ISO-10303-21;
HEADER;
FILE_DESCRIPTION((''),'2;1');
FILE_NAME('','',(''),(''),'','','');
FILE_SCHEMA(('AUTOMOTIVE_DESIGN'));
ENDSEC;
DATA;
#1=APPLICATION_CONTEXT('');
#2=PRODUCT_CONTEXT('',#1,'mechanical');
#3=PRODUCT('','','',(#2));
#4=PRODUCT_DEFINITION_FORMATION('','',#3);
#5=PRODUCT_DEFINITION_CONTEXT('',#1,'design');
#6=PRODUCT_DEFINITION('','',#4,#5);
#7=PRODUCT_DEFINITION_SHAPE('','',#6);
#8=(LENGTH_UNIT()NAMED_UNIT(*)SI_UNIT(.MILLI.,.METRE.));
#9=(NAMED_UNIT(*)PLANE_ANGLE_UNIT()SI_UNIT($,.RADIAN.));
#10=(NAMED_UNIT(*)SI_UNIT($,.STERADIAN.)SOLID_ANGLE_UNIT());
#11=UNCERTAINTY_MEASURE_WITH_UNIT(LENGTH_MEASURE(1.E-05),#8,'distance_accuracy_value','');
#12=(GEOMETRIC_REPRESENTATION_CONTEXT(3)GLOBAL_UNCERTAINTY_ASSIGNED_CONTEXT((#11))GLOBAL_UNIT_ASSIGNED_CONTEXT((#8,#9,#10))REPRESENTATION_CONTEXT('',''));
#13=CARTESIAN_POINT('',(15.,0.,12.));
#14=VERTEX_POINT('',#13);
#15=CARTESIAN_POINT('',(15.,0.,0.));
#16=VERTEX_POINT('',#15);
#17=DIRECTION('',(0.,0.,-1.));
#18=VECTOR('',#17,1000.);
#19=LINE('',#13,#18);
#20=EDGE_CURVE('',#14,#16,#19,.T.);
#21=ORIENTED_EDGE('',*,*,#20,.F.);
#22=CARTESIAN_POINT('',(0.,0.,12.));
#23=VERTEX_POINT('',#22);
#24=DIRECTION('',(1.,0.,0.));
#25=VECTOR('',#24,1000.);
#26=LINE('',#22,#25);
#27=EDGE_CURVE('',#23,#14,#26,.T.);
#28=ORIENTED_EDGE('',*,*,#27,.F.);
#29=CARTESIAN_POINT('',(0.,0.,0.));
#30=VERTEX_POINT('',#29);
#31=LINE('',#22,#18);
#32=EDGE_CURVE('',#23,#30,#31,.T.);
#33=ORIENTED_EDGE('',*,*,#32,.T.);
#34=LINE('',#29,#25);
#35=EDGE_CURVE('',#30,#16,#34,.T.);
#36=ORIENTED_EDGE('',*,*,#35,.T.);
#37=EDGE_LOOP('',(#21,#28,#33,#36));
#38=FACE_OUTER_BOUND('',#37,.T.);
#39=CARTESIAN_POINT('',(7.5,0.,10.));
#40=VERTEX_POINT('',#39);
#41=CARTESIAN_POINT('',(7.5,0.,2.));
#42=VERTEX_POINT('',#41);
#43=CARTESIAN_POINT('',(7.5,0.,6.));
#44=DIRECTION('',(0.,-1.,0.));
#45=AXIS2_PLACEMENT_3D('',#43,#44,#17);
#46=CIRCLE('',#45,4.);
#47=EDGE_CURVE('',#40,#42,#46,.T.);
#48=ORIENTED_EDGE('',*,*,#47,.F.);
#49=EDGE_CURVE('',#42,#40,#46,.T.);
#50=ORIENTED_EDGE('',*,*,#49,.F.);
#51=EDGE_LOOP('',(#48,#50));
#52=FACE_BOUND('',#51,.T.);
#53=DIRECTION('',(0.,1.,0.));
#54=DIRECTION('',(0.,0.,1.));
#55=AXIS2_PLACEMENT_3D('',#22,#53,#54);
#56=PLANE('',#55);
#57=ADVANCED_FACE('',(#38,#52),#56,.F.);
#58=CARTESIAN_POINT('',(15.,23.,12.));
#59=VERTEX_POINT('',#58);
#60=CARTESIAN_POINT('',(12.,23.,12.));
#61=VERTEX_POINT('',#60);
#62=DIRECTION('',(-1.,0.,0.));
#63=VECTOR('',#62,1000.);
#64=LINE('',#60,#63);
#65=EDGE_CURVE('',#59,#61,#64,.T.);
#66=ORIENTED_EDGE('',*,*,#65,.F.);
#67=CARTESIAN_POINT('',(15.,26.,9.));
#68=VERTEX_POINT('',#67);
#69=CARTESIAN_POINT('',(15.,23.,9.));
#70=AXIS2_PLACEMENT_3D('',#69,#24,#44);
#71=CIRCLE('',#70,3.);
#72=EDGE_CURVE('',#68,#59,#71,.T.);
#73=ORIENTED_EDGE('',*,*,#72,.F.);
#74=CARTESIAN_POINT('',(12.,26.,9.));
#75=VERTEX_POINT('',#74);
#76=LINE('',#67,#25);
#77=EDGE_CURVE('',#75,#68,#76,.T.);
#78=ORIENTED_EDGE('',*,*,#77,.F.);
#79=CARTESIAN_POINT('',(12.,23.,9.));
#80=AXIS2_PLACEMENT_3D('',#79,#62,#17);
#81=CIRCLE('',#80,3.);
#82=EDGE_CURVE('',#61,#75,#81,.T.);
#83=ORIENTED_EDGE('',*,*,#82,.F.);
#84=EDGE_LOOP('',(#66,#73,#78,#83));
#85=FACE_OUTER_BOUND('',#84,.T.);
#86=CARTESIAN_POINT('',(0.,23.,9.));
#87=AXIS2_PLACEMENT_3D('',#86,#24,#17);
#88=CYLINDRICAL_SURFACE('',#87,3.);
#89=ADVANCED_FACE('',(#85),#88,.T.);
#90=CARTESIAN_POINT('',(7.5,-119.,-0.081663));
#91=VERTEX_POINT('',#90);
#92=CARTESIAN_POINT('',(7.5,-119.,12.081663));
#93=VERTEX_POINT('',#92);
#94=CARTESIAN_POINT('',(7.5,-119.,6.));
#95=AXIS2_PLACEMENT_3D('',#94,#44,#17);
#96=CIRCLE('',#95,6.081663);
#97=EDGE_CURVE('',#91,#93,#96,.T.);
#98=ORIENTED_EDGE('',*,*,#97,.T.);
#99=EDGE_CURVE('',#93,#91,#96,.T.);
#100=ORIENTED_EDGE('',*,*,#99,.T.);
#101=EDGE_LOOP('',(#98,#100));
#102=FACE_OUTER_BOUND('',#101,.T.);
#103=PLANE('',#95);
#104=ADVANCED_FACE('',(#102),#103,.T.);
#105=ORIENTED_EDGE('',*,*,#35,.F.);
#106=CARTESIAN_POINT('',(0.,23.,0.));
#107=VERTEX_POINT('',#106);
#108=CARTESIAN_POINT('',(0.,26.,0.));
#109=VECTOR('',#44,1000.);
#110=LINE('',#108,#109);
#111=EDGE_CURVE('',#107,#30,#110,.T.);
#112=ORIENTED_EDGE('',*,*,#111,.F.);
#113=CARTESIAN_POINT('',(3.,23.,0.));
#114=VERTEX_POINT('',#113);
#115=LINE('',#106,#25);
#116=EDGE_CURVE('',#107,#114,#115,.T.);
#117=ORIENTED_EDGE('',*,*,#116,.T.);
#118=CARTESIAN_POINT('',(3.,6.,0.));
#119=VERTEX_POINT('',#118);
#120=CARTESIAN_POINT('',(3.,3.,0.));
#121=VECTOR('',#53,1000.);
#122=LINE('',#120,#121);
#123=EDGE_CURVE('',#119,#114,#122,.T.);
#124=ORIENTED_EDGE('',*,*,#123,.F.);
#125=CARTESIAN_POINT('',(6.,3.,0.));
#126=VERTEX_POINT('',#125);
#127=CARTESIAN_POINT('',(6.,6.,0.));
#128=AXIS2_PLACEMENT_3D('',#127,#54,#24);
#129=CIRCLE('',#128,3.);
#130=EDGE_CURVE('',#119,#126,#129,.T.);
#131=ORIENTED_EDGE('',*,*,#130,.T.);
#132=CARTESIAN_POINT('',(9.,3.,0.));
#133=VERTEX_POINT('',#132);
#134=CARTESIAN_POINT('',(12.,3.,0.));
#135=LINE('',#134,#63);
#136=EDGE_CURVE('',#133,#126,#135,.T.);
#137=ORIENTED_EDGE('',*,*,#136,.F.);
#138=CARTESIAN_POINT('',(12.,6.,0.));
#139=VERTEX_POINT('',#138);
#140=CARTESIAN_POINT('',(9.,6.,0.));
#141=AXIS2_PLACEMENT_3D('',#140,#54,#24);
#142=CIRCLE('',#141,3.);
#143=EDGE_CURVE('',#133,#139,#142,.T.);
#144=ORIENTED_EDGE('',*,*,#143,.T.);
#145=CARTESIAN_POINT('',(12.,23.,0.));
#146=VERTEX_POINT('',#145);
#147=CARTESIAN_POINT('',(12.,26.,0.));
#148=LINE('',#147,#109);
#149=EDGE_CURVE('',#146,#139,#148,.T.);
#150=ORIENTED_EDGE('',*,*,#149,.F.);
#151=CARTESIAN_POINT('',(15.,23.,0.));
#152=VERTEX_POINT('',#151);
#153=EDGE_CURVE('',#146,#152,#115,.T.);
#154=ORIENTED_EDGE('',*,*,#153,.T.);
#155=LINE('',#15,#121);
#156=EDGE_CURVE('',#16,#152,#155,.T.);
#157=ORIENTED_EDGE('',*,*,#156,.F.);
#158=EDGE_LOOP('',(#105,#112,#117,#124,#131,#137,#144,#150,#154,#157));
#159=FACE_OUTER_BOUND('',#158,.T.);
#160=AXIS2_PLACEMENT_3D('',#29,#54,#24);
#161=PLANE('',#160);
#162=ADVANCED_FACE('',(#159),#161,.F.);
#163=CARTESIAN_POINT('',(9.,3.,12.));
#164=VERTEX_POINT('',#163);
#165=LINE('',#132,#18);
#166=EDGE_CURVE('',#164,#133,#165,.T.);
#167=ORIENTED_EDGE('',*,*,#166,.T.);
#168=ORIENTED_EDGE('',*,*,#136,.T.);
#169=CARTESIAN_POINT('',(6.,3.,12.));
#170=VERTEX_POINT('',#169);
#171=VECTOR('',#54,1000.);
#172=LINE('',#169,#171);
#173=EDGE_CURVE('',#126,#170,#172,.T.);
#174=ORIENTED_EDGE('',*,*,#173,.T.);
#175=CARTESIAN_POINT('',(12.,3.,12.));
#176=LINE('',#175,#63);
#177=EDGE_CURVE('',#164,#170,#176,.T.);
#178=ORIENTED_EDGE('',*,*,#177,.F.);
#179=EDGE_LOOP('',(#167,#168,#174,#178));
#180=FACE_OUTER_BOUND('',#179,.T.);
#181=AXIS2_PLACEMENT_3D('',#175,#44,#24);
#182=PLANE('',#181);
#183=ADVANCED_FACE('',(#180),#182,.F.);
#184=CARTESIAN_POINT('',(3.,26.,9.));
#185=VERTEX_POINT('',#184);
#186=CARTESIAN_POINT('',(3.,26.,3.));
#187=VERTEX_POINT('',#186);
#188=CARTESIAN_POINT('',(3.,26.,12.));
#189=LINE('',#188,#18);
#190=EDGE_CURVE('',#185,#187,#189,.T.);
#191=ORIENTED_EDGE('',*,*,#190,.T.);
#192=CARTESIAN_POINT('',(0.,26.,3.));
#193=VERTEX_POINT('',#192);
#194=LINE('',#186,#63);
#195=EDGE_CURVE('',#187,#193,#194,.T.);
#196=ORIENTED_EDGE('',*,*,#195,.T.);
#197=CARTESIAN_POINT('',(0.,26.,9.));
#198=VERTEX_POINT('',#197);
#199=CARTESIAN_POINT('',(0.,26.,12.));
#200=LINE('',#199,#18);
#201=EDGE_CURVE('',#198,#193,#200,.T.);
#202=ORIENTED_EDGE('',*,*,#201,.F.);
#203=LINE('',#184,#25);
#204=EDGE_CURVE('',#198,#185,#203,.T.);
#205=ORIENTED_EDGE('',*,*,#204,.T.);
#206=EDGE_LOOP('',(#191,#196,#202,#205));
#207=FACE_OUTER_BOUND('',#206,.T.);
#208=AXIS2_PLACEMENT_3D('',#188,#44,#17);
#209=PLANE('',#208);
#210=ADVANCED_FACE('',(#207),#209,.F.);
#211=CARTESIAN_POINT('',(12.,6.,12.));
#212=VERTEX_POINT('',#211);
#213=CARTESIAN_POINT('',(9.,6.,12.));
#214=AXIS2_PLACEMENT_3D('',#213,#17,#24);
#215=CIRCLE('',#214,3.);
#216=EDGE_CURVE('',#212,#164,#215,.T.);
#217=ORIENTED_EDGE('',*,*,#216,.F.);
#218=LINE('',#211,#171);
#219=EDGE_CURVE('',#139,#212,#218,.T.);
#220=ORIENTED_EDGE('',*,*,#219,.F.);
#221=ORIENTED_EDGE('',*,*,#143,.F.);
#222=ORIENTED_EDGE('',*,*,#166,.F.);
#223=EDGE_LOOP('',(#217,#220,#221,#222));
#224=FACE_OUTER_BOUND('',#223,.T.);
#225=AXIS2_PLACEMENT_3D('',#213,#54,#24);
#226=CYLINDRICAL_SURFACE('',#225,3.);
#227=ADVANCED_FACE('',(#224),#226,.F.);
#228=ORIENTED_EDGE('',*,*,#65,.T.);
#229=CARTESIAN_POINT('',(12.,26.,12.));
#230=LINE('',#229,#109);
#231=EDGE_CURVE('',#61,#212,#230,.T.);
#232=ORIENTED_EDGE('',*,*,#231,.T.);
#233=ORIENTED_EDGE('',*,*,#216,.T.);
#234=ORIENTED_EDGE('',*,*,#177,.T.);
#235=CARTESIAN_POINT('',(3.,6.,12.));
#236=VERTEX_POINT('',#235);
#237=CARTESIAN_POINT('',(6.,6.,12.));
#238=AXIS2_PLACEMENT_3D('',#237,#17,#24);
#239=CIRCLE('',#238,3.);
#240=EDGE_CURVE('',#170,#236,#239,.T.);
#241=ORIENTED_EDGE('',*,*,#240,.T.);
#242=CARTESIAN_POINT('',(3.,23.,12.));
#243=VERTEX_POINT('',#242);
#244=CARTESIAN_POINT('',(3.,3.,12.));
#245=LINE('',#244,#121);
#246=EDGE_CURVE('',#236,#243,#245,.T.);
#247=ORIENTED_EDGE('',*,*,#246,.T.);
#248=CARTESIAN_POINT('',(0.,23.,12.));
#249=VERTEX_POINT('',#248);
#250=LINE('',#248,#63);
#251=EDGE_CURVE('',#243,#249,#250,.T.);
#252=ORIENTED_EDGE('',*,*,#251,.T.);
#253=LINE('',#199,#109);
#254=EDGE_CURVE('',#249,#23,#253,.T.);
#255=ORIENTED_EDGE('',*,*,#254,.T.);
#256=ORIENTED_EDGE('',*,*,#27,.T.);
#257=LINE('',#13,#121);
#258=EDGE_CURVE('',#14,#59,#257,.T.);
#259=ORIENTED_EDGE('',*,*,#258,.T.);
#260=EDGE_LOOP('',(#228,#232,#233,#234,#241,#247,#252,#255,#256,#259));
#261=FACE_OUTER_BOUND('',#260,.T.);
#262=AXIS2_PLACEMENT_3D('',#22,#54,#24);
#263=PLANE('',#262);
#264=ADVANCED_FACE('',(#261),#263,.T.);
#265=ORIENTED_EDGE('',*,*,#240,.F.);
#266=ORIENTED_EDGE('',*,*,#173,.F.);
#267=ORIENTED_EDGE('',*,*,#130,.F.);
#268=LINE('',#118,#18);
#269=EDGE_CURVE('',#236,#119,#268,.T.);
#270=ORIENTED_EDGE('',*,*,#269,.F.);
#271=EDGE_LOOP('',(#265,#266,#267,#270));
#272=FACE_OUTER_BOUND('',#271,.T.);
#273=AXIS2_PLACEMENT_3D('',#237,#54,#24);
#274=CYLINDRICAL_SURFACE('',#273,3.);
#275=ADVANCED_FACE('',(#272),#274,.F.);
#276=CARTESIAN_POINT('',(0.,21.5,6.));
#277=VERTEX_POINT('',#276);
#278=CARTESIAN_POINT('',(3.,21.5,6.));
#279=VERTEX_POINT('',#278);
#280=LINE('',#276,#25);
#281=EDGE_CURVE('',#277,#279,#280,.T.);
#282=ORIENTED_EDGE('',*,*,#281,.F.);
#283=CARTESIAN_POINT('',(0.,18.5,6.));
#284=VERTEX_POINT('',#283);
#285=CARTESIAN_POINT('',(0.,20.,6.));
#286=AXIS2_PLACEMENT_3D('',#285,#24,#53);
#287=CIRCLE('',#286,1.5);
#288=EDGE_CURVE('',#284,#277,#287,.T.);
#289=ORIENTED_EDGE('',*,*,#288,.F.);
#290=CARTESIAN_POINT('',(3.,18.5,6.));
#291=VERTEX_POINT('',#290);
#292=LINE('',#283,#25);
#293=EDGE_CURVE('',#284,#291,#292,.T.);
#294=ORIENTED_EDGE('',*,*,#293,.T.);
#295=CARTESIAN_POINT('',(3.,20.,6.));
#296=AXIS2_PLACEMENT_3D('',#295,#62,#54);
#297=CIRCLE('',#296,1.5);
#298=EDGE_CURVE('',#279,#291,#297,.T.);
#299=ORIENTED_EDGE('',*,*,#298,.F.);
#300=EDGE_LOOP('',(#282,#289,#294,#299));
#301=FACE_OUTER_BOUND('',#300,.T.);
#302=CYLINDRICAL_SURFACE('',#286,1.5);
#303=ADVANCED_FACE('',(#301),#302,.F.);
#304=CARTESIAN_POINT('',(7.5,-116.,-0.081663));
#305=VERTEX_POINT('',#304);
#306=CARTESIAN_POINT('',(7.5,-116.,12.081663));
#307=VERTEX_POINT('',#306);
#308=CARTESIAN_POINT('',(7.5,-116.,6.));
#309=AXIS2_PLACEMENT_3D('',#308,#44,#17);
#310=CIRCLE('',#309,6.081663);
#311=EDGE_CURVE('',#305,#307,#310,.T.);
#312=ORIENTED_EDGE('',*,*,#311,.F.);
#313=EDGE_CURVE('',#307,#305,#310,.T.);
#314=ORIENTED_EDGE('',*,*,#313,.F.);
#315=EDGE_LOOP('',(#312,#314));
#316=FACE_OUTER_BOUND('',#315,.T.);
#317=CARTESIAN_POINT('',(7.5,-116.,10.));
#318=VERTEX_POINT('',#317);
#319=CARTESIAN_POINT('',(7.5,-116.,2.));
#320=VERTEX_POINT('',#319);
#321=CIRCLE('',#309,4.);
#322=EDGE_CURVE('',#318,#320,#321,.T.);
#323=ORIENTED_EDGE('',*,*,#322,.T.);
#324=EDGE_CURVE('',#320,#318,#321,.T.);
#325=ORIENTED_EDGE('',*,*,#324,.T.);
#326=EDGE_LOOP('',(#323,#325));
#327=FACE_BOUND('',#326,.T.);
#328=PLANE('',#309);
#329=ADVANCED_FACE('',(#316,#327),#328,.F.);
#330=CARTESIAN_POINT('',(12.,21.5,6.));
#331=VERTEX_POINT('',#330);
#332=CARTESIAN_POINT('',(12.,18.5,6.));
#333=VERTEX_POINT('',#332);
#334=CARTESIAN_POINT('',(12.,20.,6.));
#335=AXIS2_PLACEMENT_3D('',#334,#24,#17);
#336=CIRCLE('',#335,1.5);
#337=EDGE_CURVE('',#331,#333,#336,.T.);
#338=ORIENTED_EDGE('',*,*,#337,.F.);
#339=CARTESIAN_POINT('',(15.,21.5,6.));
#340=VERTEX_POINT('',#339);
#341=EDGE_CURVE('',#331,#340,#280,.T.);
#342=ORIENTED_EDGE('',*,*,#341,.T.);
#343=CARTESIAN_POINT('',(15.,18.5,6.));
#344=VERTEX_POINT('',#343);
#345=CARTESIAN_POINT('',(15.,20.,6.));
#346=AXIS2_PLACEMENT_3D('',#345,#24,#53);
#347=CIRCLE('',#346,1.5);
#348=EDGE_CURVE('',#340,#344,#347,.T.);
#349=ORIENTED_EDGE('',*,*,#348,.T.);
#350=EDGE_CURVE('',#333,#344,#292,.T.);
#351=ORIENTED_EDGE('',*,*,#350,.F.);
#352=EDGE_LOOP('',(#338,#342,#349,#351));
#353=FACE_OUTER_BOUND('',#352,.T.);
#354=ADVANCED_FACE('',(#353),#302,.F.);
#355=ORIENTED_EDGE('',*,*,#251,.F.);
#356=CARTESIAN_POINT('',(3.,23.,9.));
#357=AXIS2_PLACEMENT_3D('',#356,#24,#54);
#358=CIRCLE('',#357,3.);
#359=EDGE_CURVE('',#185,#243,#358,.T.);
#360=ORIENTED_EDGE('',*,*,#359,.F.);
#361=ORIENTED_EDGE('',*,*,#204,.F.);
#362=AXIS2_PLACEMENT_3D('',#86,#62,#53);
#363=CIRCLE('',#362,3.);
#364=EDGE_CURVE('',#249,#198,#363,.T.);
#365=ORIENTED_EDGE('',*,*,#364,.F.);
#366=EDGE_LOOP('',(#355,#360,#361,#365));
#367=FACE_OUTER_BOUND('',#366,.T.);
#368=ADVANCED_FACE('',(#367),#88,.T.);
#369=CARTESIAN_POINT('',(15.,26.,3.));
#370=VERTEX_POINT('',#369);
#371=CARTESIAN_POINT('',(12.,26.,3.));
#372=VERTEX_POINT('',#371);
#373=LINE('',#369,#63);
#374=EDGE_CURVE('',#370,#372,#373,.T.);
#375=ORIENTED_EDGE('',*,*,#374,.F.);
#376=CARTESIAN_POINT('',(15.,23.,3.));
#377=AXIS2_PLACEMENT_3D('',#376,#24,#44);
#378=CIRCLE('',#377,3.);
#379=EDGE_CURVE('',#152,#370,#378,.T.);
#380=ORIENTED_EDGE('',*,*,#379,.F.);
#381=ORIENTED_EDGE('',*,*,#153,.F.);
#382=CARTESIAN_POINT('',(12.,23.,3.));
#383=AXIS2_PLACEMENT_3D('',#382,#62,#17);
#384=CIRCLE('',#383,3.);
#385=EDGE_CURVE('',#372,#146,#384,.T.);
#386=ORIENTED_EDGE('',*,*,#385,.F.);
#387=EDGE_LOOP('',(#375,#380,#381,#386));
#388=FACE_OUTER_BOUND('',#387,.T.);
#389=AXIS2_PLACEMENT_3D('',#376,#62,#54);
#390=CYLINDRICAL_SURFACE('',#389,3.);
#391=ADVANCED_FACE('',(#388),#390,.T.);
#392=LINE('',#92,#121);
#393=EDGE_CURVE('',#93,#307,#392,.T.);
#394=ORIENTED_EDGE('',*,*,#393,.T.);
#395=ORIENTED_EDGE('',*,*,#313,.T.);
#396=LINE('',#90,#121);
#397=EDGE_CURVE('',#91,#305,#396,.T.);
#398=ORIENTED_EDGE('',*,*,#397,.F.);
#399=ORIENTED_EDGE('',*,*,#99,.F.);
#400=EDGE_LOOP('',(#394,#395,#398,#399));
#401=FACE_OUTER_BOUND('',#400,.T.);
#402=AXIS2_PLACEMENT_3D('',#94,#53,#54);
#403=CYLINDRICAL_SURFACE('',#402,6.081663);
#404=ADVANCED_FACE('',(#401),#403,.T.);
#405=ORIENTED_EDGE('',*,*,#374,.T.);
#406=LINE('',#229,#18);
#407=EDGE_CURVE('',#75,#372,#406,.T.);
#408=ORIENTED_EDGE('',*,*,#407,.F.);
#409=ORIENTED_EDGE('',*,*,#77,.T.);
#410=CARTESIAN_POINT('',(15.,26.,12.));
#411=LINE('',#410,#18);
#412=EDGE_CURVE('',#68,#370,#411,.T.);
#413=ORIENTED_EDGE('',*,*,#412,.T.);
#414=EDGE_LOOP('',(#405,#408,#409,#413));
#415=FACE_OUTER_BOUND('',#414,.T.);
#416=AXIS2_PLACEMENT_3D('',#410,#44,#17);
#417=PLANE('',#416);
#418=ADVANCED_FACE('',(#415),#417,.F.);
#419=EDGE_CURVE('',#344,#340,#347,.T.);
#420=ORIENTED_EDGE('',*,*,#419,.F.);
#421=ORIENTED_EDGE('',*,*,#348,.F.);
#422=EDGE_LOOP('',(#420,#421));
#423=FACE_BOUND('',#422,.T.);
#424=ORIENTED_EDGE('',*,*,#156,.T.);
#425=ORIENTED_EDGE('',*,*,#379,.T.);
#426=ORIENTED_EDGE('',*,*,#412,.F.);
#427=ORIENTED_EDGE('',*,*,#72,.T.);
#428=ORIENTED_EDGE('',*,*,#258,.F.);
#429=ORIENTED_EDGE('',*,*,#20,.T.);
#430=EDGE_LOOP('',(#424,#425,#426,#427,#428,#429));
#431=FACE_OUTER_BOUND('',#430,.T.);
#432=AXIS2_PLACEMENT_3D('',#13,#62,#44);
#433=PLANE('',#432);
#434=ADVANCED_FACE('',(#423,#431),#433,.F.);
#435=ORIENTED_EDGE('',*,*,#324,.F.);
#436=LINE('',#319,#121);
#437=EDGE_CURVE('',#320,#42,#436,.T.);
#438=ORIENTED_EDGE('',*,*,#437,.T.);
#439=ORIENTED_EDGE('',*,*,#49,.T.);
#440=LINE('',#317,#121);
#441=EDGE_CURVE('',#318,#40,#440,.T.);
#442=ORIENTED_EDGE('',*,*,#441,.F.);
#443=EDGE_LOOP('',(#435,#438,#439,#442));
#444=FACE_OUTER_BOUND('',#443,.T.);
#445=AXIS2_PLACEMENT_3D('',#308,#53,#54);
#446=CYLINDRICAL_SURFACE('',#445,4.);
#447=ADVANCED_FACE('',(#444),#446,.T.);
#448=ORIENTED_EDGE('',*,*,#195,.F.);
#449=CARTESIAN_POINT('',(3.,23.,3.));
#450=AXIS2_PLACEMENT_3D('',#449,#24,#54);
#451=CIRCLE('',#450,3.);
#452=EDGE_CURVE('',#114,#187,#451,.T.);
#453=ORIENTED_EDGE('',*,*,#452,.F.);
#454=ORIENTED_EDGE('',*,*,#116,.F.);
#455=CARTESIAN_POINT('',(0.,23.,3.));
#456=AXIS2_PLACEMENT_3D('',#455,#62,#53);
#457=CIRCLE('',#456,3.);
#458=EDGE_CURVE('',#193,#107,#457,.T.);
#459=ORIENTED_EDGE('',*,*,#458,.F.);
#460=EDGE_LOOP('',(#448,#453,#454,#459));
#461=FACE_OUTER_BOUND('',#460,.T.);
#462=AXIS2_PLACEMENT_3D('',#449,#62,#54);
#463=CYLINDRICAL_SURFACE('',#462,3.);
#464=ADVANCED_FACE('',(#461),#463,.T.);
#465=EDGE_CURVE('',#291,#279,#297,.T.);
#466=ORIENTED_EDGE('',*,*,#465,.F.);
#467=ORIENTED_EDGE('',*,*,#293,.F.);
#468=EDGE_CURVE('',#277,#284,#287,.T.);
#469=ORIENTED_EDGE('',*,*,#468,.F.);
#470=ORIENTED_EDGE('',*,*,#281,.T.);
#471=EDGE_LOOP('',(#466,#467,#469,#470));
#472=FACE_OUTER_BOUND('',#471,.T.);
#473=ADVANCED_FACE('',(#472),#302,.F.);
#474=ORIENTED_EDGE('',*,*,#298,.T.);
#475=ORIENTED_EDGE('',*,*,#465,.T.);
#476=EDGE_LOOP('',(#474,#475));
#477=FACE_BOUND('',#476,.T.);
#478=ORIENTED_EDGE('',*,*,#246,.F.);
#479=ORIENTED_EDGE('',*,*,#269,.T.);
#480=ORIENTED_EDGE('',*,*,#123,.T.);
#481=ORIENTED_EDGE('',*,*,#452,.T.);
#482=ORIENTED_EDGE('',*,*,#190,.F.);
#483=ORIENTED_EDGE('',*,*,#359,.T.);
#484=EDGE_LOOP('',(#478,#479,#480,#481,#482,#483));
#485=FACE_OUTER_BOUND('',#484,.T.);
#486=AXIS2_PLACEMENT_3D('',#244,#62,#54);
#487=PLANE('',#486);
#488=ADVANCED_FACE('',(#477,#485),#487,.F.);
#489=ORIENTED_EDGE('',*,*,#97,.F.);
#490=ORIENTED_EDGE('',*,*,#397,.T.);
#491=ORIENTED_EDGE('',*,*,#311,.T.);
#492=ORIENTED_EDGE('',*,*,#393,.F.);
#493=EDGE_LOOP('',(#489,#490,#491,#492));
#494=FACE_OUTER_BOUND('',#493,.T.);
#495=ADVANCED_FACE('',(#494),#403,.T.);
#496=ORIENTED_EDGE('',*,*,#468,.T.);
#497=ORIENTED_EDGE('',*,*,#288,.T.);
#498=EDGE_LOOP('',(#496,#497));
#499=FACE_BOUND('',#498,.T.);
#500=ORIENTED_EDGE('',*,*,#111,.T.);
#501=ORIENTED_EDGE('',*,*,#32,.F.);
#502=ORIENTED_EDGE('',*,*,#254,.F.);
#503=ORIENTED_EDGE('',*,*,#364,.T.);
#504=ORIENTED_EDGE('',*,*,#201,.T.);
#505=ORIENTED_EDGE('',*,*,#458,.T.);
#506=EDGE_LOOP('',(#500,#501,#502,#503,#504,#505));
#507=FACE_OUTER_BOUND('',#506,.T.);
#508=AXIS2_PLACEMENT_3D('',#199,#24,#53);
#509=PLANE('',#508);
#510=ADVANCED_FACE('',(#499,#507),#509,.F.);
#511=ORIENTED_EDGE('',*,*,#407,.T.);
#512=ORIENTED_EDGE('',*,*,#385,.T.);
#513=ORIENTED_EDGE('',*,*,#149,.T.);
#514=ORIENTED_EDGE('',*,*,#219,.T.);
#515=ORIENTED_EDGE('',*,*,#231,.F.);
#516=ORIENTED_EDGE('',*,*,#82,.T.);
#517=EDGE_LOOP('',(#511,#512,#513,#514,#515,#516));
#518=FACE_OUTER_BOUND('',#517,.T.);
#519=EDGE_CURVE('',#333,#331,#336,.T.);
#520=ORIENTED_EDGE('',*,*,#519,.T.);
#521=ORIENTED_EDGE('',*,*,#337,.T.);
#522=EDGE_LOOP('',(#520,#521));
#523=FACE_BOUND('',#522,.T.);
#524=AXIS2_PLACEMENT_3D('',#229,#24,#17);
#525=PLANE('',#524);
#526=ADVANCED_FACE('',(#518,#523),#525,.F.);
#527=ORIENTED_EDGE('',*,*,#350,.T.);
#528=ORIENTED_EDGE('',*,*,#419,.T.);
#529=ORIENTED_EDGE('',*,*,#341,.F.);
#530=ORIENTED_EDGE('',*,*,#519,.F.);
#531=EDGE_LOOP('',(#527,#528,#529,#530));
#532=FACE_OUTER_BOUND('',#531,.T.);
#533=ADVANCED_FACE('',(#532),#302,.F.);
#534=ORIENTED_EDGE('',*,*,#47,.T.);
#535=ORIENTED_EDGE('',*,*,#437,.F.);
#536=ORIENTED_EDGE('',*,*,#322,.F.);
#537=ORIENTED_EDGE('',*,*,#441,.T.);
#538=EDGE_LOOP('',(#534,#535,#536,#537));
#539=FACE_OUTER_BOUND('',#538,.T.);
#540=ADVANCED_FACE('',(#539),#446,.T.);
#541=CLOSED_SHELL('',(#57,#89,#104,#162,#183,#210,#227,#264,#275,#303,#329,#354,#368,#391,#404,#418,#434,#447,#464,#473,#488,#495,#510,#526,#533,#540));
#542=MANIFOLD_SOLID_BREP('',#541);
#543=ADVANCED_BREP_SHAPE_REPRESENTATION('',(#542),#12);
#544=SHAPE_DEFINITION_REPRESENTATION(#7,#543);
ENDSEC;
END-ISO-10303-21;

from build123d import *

# Parameters (mm, degrees)
BOSS_EXTRUDE1_DEPTH = 12
FILLET1_R           = 3
FILLET2_R           = 3
SKETCH2_R           = 1.5
CUT_EXTRUDE1_DEPTH  = 33.32645975
SKETCH3_R           = 4
BOSS_EXTRUDE2_DEPTH = 116
SKETCH4_R           = 6.081663029
BOSS_EXTRUDE3_DEPTH = 3


with BuildPart() as part:
    # Sketch1 → Boss-Extrude1 (new body)
    with BuildSketch(Plane.XY):
        Polygon((0, 26), (0, 0), (15, 0), (15, 26), (12, 26), (12, 3), (3, 3), (3, 26), align=None)
    extrude(amount=BOSS_EXTRUDE1_DEPTH)

    # Fillet1
    fillet1_edges = [part.edges().sort_by_distance(p)[0] for p in [
        (1.5, 26, 0),
        (13.5, 26, 12),
        (1.5, 26, 12),
        (13.5, 26, 0),
    ]]
    fillet(fillet1_edges, radius=FILLET1_R)

    # Fillet2
    fillet2_edges = [part.edges().sort_by_distance(p)[0] for p in [
        (3, 3, 6),
        (12, 3, 6),
    ]]
    fillet(fillet2_edges, radius=FILLET2_R)

    # Sketch2 → Cut-Extrude1 (cut, through all)
    with BuildSketch(Plane(origin=(15, 0, 0), x_dir=(0, 0, -1), z_dir=(1, 0, 0))):
        with Locations(Location((-6, 20, 0), (0, 0, 90))):
            Circle(SKETCH2_R)
    extrude(amount=-CUT_EXTRUDE1_DEPTH, mode=Mode.SUBTRACT)

    # Sketch3 → Boss-Extrude2 (add)
    with BuildSketch(Plane(origin=(0, 0, 0), x_dir=(-1, 0, 0), z_dir=(0, -1, 0))):
        with Locations(Location((-7.5, -6, 0), (0, 0, 270))):
            Circle(SKETCH3_R)
    extrude(amount=BOSS_EXTRUDE2_DEPTH)

    # Sketch4 → Boss-Extrude3 (add)
    with BuildSketch(Plane(origin=(0, -116, 0), x_dir=(-1, 0, 0), z_dir=(0, -1, 0))):
        with Locations(Location((-7.5, -6, 0), (0, 0, 90))):
            Circle(SKETCH4_R)
    extrude(amount=BOSS_EXTRUDE3_DEPTH)


solid = part.part
